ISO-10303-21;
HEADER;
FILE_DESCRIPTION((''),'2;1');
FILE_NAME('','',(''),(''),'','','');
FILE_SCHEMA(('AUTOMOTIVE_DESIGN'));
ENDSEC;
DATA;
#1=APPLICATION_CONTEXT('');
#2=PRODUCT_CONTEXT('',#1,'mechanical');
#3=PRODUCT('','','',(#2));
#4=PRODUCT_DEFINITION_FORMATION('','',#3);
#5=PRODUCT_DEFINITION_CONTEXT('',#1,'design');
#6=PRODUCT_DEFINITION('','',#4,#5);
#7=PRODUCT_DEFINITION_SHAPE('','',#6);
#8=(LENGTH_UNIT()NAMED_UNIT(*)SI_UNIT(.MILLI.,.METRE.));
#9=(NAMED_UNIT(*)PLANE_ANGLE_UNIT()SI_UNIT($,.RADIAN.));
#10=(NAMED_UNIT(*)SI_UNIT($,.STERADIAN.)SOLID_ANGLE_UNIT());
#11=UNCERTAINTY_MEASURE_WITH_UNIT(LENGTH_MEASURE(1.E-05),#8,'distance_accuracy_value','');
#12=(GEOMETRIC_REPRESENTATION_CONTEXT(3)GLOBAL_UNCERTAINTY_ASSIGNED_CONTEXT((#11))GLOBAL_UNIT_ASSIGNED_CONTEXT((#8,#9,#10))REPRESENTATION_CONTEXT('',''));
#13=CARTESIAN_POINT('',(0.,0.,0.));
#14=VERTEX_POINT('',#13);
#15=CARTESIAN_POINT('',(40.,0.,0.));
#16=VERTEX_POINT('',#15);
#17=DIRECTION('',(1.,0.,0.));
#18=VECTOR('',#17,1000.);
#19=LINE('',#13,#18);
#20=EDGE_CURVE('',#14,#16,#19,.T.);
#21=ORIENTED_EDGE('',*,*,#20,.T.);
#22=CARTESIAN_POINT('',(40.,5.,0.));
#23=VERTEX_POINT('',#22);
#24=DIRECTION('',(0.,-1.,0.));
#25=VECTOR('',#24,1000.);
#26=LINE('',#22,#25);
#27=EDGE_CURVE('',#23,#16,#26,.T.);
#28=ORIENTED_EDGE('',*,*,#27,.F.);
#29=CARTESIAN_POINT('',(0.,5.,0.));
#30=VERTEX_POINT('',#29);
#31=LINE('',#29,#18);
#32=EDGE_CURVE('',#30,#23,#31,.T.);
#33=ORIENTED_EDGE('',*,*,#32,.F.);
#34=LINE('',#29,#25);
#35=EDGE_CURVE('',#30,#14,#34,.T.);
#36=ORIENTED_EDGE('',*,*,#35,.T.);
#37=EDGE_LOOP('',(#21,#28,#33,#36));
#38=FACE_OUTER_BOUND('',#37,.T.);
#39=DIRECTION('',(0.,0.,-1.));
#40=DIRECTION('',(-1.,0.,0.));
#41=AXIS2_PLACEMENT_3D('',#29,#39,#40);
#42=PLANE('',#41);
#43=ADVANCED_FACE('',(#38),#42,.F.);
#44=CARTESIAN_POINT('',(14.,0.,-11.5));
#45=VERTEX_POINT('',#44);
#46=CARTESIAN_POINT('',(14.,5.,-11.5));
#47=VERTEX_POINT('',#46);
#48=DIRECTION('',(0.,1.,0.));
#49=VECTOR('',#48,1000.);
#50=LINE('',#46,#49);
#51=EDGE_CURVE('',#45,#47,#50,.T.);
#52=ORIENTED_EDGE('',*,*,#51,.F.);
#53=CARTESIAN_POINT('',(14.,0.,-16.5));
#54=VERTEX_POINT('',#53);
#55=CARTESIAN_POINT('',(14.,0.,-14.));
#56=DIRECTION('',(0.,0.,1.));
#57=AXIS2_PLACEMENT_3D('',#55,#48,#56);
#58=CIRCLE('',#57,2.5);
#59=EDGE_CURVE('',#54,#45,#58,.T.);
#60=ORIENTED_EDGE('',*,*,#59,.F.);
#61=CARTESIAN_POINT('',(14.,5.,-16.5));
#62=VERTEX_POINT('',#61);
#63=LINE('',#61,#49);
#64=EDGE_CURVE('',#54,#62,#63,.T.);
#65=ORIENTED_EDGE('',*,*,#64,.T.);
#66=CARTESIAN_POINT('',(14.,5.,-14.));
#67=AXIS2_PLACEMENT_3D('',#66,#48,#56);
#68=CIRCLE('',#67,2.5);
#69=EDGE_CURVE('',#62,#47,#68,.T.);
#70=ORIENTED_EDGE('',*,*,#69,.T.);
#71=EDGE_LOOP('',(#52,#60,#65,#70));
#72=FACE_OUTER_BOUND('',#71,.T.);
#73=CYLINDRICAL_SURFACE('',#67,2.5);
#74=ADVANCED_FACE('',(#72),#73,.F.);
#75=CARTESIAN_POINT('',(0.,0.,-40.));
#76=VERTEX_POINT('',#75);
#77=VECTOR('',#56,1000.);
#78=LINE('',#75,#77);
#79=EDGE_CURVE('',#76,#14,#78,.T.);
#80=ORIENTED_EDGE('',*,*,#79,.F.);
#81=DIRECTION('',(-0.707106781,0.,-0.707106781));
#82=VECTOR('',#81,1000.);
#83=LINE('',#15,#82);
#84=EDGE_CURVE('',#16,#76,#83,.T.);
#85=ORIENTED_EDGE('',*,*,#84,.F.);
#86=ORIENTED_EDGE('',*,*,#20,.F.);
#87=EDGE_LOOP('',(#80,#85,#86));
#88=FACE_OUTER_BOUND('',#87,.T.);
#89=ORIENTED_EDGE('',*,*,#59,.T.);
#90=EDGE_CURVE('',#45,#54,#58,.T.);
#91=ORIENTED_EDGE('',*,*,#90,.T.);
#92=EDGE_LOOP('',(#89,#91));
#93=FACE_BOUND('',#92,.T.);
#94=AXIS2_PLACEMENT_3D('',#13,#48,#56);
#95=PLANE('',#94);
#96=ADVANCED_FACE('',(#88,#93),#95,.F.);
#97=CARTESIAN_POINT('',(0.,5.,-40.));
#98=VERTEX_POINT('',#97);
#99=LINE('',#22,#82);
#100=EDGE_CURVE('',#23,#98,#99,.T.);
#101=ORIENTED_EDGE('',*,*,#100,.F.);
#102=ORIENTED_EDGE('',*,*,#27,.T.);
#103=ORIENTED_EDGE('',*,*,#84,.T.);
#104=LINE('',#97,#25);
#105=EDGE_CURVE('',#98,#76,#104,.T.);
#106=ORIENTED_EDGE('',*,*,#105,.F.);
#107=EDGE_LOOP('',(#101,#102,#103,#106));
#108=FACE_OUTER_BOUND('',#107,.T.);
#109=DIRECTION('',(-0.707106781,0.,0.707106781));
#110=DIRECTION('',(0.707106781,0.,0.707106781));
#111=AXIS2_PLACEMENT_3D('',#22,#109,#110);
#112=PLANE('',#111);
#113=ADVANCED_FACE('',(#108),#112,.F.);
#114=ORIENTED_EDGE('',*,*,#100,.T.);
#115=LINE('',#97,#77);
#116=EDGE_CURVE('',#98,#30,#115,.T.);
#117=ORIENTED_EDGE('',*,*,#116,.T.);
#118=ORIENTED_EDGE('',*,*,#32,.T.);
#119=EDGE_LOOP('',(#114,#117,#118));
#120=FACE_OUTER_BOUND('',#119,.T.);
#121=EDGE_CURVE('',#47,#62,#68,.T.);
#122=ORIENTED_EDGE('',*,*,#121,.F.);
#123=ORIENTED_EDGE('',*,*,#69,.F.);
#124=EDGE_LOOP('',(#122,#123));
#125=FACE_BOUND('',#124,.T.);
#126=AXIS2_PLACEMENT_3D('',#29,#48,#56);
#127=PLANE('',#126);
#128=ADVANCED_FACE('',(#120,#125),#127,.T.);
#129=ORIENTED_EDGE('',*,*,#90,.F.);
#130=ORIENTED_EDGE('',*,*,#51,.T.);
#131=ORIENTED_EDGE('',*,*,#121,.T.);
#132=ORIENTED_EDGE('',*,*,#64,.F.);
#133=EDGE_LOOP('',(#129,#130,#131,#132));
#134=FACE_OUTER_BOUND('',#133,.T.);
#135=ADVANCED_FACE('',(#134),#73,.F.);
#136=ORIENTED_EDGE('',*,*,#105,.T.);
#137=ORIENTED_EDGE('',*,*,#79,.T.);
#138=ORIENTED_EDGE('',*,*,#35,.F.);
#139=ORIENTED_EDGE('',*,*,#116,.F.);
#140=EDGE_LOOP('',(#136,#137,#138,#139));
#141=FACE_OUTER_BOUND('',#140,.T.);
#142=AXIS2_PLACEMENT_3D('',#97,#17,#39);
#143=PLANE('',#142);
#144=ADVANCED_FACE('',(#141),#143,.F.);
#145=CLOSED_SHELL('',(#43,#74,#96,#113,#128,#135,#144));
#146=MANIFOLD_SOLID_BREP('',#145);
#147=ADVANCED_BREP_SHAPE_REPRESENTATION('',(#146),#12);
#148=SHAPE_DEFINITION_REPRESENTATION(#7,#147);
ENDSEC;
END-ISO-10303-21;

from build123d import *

# Parameters (mm, degrees)
EXTRUDE_1_DEPTH        = 5
HOLE_WIZARD_M6_1_D     = 5
HOLE_WIZARD_M6_1_DEPTH = 15
HOLE_WIZARD_M6_1_TIP   = 1.502151548


with BuildPart() as part:
    # 草图1 → 凸台-拉伸1 (new body)
    with BuildSketch(Plane(origin=(0, 0, 0), x_dir=(1, 0, 0), z_dir=(0, 1, 0))):
        Polygon((0, 40), (0, 0), (40, 0), align=None)
    extrude(amount=EXTRUDE_1_DEPTH)

    # M6 螺纹孔1
    with Locations(Plane(origin=(0, 5, 0), x_dir=(1, 0, 0), z_dir=(0, 1, 0))):
        with Locations((14, 14)):
            Hole(HOLE_WIZARD_M6_1_D / 2, depth=HOLE_WIZARD_M6_1_DEPTH)
            with Locations((0, 0, -(HOLE_WIZARD_M6_1_DEPTH + HOLE_WIZARD_M6_1_TIP / 2))):  # 118° drill point
                Cone(0, HOLE_WIZARD_M6_1_D / 2, HOLE_WIZARD_M6_1_TIP, mode=Mode.SUBTRACT)


solid = part.part
